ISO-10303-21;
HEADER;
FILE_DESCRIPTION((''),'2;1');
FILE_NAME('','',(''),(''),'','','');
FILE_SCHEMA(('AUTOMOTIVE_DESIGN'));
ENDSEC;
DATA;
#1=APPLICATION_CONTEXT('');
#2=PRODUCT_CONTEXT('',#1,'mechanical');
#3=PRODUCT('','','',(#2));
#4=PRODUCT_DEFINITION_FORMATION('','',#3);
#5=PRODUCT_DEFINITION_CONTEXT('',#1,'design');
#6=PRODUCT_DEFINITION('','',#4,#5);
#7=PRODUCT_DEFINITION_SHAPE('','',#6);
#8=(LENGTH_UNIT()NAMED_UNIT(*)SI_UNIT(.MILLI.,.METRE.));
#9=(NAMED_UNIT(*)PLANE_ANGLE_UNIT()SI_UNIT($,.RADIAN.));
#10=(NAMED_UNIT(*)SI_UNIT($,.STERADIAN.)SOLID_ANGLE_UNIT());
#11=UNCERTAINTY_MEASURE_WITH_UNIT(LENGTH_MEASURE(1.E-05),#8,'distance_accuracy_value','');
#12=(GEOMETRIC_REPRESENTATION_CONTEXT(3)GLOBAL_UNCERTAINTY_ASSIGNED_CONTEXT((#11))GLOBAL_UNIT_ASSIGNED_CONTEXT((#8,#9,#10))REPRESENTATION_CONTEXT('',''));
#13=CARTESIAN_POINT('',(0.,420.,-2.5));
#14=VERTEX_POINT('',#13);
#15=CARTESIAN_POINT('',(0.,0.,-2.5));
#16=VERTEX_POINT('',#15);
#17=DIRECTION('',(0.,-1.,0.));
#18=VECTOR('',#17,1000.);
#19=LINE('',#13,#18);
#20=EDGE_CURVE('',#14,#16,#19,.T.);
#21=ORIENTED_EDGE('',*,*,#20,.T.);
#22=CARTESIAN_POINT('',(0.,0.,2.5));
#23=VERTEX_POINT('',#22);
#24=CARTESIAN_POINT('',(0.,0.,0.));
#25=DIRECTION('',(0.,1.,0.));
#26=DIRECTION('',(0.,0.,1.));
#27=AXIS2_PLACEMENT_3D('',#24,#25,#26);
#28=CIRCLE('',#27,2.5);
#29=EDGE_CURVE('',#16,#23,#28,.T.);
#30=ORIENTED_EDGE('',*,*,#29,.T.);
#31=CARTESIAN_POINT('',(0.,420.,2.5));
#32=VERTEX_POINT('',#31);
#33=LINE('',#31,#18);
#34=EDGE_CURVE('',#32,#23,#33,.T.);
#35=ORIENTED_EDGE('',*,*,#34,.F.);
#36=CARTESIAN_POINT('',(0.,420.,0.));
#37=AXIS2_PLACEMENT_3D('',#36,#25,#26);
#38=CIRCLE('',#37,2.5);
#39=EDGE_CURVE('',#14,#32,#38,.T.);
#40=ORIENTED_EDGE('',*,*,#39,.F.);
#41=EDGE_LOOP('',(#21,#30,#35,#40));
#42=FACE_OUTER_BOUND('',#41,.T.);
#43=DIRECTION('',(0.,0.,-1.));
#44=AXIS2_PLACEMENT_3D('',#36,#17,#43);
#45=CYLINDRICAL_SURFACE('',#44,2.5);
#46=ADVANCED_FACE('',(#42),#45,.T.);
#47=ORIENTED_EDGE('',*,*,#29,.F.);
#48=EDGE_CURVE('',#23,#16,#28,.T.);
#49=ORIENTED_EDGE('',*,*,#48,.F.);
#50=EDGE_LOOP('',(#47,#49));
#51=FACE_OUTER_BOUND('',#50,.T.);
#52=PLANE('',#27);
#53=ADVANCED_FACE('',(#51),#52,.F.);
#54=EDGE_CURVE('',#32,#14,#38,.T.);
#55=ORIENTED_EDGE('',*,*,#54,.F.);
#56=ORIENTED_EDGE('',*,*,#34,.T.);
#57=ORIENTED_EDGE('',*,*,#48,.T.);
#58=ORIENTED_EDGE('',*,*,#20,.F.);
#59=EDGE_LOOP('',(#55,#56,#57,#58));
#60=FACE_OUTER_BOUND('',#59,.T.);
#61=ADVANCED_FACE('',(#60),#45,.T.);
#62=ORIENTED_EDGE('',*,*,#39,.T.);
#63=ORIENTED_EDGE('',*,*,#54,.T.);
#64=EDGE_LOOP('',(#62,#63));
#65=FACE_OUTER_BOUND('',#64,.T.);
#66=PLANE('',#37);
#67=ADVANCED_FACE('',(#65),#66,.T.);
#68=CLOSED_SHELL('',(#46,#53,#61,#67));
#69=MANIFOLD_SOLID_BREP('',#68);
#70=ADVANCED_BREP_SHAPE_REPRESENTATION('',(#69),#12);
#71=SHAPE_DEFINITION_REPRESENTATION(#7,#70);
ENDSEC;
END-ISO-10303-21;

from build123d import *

# Parameters (mm, degrees)
SKETCH1_R           = 2.5
BOSS_EXTRUDE1_DEPTH = 420


with BuildPart() as part:
    # Sketch1 → Boss-Extrude1 (new body)
    with BuildSketch(Plane(origin=(0, 0, 0), x_dir=(1, 0, 0), z_dir=(0, 1, 0))):
        with Locations(Location((0, 0, 0), (0, 0, 270))):
            Circle(SKETCH1_R)
    extrude(amount=BOSS_EXTRUDE1_DEPTH)


solid = part.part
